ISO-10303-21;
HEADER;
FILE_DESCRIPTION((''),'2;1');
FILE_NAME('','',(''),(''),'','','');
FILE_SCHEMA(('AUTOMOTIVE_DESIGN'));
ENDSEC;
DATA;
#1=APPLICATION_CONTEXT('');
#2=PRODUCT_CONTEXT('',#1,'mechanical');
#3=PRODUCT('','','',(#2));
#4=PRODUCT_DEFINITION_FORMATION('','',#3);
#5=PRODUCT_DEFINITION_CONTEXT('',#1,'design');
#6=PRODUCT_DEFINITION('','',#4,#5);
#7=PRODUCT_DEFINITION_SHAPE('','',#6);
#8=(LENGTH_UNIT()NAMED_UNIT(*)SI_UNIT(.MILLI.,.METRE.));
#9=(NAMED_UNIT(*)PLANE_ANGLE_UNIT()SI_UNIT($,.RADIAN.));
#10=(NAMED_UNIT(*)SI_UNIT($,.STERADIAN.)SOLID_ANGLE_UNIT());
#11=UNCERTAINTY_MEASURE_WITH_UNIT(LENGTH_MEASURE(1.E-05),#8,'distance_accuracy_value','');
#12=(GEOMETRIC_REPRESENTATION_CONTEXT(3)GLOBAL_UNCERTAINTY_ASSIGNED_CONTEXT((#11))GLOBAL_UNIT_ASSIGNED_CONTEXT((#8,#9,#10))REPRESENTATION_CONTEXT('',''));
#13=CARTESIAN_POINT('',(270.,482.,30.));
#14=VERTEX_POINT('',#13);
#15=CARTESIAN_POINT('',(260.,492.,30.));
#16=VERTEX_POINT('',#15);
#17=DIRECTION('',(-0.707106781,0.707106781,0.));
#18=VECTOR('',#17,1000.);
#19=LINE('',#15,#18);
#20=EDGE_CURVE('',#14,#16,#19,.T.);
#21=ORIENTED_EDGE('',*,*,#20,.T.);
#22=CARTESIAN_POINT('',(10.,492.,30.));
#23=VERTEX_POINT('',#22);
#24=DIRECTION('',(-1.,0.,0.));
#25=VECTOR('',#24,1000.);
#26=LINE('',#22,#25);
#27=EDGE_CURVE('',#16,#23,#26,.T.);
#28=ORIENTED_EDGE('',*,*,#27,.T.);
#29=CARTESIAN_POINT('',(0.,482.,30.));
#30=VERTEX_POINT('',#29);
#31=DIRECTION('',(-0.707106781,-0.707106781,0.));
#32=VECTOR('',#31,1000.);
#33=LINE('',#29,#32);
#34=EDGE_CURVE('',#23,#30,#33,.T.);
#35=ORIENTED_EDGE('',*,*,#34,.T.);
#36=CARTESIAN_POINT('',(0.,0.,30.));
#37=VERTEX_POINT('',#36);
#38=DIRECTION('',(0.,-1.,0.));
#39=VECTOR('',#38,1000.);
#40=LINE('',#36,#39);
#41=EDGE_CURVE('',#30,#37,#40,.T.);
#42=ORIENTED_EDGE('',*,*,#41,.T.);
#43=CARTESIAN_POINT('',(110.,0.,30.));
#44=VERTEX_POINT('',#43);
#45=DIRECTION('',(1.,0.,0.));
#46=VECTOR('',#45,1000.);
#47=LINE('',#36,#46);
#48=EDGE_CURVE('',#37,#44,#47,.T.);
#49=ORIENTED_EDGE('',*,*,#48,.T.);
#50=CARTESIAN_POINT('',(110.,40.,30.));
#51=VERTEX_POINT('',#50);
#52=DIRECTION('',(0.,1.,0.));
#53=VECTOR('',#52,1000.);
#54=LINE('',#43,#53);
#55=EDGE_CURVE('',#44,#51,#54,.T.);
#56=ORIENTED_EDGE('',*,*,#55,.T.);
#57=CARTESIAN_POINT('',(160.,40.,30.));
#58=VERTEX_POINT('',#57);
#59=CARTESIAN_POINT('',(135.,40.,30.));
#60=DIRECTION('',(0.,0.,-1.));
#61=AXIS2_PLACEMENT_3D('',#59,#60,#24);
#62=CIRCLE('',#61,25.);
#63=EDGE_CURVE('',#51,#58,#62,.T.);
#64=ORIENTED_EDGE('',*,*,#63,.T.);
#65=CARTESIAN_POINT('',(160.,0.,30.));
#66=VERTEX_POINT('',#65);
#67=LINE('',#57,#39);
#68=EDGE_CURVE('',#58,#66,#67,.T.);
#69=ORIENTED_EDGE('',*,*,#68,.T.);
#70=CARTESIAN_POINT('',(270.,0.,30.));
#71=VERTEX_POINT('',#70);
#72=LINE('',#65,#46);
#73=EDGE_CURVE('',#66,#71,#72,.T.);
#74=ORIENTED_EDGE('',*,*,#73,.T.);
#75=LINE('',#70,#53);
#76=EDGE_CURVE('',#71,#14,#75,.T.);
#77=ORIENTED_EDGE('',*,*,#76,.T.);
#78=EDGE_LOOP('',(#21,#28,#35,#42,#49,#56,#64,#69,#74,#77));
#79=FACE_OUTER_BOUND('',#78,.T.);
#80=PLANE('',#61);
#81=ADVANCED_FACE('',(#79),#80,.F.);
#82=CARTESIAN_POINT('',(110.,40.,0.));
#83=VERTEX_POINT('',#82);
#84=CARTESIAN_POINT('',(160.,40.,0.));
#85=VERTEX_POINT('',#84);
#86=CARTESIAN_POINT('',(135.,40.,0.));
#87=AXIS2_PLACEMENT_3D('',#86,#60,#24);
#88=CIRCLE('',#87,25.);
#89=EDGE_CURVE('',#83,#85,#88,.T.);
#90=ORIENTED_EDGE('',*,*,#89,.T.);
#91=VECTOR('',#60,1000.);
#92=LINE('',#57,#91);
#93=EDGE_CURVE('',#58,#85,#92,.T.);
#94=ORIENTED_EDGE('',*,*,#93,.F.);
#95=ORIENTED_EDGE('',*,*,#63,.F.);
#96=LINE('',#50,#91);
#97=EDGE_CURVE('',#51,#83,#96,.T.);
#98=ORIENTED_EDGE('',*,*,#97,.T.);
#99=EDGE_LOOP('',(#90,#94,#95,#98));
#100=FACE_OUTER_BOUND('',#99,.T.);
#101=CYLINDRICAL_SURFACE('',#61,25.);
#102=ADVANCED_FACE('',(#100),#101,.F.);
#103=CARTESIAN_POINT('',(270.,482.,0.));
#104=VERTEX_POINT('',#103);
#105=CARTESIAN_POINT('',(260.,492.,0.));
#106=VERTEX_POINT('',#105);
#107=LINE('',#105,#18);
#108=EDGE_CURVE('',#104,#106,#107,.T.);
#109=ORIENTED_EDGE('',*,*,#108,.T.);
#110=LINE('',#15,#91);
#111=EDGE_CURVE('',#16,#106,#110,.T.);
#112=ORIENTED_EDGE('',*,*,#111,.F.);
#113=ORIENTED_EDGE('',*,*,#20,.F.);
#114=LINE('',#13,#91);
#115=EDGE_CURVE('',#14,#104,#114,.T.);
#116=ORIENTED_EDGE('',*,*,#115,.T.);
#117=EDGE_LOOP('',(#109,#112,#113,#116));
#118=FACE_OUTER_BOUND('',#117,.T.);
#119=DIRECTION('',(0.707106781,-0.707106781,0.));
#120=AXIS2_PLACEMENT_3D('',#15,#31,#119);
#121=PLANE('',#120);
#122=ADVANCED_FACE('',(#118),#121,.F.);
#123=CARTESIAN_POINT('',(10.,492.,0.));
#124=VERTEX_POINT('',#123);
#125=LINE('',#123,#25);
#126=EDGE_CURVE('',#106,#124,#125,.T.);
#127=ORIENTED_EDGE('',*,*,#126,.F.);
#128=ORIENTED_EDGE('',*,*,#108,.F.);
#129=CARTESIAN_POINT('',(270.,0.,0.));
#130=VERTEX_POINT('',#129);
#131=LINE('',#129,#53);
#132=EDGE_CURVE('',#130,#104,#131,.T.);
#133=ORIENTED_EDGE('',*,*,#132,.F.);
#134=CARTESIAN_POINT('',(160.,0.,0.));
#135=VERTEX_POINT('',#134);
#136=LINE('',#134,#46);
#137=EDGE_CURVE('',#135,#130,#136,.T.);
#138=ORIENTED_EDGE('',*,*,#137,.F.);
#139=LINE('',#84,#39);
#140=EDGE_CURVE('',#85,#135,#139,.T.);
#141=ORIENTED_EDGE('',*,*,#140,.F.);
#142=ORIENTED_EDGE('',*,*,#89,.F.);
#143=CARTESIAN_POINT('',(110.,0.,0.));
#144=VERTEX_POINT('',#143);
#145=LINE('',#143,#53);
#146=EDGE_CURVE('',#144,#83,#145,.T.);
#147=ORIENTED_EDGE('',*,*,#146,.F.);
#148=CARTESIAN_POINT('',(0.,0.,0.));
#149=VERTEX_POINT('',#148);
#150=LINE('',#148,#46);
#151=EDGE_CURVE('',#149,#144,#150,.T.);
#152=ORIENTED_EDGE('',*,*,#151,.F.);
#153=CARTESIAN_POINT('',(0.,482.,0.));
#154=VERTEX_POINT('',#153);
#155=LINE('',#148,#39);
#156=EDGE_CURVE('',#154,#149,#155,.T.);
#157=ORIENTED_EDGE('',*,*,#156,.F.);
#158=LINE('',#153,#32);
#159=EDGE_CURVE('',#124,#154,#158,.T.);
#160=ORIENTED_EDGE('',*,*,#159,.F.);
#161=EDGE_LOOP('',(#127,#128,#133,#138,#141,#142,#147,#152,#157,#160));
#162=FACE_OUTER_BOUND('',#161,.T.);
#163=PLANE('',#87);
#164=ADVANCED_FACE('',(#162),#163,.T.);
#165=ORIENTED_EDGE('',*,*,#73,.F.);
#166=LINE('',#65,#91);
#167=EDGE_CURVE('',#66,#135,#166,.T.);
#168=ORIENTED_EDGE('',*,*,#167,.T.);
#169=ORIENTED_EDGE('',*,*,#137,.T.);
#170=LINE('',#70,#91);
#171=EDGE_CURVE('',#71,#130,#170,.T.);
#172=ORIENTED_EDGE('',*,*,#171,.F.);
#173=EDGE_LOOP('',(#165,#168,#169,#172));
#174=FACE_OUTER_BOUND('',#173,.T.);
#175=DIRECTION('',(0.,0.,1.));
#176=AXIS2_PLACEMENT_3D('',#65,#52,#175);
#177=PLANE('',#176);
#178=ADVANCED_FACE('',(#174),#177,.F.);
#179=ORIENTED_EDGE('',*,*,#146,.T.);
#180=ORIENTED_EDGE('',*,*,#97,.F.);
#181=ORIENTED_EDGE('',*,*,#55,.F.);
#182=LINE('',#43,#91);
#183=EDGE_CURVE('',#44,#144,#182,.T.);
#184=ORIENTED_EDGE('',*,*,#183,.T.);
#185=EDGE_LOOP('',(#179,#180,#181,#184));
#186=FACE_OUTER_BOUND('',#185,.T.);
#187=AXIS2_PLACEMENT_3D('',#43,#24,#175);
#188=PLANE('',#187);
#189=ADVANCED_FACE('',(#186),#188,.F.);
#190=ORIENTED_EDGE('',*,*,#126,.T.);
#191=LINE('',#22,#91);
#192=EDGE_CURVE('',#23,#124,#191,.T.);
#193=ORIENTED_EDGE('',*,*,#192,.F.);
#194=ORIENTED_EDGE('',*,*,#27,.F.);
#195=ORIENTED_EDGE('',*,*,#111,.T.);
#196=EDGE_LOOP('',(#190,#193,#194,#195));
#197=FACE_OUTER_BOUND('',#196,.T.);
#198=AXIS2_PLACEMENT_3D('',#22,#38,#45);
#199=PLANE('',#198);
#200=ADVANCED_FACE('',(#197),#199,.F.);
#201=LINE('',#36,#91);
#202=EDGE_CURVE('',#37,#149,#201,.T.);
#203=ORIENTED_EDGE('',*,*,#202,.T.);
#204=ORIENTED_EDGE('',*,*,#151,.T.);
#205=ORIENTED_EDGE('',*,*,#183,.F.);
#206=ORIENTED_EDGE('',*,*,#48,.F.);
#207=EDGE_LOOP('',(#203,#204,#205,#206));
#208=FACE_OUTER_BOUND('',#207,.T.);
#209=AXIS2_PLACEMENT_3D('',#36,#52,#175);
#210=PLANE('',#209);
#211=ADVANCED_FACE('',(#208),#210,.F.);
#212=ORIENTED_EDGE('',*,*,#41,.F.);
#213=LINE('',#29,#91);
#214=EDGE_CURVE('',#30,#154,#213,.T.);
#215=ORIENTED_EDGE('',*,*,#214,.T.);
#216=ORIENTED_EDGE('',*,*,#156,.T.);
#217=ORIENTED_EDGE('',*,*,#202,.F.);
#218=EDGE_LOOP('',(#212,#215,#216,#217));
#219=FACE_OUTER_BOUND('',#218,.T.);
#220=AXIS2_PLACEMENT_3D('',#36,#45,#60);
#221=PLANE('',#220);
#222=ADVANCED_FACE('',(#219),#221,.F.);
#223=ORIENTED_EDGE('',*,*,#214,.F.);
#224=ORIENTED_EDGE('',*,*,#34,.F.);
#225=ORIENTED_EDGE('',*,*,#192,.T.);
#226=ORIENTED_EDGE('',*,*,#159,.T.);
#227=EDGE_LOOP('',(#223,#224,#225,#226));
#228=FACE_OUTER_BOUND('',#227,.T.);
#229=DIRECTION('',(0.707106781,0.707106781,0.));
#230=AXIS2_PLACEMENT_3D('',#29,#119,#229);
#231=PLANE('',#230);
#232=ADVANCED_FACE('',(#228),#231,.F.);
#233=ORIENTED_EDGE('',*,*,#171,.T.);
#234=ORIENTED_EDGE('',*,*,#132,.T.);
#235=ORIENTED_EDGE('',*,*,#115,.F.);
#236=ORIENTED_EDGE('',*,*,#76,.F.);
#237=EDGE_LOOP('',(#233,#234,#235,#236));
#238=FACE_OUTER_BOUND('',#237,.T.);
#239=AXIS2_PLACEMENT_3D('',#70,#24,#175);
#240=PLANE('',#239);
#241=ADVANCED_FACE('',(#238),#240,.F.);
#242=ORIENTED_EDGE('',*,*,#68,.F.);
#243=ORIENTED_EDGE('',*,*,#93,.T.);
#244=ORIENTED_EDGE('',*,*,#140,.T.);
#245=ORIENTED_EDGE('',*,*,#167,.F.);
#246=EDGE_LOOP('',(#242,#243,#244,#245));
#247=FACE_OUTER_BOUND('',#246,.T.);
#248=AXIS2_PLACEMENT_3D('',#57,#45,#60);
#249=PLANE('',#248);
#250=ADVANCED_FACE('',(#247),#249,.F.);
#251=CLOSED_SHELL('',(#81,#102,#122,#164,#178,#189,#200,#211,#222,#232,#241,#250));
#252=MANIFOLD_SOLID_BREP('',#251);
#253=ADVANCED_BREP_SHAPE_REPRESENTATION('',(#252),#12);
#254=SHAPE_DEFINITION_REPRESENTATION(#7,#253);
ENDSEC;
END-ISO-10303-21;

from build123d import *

# Parameters (mm, degrees)
BOSS_EXTRUDE1_DEPTH = 30


with BuildPart() as part:
    # Sketch1 → Boss-Extrude1 (new body)
    with BuildSketch(Plane.XY):
        with BuildLine():
            Line((110, 0), (110, 40))
            ThreePointArc((110, 40), (135, 65), (160, 40))
            Line((160, 40), (160, 0))
            Line((160, 0), (270, 0))
            Line((270, 0), (270, 482))
            Line((270, 482), (260, 492))
            Line((260, 492), (10, 492))
            Line((10, 492), (0, 482))
            Line((0, 482), (0, 0))
            Line((0, 0), (110, 0))
        make_face()
    extrude(amount=BOSS_EXTRUDE1_DEPTH)


solid = part.part
